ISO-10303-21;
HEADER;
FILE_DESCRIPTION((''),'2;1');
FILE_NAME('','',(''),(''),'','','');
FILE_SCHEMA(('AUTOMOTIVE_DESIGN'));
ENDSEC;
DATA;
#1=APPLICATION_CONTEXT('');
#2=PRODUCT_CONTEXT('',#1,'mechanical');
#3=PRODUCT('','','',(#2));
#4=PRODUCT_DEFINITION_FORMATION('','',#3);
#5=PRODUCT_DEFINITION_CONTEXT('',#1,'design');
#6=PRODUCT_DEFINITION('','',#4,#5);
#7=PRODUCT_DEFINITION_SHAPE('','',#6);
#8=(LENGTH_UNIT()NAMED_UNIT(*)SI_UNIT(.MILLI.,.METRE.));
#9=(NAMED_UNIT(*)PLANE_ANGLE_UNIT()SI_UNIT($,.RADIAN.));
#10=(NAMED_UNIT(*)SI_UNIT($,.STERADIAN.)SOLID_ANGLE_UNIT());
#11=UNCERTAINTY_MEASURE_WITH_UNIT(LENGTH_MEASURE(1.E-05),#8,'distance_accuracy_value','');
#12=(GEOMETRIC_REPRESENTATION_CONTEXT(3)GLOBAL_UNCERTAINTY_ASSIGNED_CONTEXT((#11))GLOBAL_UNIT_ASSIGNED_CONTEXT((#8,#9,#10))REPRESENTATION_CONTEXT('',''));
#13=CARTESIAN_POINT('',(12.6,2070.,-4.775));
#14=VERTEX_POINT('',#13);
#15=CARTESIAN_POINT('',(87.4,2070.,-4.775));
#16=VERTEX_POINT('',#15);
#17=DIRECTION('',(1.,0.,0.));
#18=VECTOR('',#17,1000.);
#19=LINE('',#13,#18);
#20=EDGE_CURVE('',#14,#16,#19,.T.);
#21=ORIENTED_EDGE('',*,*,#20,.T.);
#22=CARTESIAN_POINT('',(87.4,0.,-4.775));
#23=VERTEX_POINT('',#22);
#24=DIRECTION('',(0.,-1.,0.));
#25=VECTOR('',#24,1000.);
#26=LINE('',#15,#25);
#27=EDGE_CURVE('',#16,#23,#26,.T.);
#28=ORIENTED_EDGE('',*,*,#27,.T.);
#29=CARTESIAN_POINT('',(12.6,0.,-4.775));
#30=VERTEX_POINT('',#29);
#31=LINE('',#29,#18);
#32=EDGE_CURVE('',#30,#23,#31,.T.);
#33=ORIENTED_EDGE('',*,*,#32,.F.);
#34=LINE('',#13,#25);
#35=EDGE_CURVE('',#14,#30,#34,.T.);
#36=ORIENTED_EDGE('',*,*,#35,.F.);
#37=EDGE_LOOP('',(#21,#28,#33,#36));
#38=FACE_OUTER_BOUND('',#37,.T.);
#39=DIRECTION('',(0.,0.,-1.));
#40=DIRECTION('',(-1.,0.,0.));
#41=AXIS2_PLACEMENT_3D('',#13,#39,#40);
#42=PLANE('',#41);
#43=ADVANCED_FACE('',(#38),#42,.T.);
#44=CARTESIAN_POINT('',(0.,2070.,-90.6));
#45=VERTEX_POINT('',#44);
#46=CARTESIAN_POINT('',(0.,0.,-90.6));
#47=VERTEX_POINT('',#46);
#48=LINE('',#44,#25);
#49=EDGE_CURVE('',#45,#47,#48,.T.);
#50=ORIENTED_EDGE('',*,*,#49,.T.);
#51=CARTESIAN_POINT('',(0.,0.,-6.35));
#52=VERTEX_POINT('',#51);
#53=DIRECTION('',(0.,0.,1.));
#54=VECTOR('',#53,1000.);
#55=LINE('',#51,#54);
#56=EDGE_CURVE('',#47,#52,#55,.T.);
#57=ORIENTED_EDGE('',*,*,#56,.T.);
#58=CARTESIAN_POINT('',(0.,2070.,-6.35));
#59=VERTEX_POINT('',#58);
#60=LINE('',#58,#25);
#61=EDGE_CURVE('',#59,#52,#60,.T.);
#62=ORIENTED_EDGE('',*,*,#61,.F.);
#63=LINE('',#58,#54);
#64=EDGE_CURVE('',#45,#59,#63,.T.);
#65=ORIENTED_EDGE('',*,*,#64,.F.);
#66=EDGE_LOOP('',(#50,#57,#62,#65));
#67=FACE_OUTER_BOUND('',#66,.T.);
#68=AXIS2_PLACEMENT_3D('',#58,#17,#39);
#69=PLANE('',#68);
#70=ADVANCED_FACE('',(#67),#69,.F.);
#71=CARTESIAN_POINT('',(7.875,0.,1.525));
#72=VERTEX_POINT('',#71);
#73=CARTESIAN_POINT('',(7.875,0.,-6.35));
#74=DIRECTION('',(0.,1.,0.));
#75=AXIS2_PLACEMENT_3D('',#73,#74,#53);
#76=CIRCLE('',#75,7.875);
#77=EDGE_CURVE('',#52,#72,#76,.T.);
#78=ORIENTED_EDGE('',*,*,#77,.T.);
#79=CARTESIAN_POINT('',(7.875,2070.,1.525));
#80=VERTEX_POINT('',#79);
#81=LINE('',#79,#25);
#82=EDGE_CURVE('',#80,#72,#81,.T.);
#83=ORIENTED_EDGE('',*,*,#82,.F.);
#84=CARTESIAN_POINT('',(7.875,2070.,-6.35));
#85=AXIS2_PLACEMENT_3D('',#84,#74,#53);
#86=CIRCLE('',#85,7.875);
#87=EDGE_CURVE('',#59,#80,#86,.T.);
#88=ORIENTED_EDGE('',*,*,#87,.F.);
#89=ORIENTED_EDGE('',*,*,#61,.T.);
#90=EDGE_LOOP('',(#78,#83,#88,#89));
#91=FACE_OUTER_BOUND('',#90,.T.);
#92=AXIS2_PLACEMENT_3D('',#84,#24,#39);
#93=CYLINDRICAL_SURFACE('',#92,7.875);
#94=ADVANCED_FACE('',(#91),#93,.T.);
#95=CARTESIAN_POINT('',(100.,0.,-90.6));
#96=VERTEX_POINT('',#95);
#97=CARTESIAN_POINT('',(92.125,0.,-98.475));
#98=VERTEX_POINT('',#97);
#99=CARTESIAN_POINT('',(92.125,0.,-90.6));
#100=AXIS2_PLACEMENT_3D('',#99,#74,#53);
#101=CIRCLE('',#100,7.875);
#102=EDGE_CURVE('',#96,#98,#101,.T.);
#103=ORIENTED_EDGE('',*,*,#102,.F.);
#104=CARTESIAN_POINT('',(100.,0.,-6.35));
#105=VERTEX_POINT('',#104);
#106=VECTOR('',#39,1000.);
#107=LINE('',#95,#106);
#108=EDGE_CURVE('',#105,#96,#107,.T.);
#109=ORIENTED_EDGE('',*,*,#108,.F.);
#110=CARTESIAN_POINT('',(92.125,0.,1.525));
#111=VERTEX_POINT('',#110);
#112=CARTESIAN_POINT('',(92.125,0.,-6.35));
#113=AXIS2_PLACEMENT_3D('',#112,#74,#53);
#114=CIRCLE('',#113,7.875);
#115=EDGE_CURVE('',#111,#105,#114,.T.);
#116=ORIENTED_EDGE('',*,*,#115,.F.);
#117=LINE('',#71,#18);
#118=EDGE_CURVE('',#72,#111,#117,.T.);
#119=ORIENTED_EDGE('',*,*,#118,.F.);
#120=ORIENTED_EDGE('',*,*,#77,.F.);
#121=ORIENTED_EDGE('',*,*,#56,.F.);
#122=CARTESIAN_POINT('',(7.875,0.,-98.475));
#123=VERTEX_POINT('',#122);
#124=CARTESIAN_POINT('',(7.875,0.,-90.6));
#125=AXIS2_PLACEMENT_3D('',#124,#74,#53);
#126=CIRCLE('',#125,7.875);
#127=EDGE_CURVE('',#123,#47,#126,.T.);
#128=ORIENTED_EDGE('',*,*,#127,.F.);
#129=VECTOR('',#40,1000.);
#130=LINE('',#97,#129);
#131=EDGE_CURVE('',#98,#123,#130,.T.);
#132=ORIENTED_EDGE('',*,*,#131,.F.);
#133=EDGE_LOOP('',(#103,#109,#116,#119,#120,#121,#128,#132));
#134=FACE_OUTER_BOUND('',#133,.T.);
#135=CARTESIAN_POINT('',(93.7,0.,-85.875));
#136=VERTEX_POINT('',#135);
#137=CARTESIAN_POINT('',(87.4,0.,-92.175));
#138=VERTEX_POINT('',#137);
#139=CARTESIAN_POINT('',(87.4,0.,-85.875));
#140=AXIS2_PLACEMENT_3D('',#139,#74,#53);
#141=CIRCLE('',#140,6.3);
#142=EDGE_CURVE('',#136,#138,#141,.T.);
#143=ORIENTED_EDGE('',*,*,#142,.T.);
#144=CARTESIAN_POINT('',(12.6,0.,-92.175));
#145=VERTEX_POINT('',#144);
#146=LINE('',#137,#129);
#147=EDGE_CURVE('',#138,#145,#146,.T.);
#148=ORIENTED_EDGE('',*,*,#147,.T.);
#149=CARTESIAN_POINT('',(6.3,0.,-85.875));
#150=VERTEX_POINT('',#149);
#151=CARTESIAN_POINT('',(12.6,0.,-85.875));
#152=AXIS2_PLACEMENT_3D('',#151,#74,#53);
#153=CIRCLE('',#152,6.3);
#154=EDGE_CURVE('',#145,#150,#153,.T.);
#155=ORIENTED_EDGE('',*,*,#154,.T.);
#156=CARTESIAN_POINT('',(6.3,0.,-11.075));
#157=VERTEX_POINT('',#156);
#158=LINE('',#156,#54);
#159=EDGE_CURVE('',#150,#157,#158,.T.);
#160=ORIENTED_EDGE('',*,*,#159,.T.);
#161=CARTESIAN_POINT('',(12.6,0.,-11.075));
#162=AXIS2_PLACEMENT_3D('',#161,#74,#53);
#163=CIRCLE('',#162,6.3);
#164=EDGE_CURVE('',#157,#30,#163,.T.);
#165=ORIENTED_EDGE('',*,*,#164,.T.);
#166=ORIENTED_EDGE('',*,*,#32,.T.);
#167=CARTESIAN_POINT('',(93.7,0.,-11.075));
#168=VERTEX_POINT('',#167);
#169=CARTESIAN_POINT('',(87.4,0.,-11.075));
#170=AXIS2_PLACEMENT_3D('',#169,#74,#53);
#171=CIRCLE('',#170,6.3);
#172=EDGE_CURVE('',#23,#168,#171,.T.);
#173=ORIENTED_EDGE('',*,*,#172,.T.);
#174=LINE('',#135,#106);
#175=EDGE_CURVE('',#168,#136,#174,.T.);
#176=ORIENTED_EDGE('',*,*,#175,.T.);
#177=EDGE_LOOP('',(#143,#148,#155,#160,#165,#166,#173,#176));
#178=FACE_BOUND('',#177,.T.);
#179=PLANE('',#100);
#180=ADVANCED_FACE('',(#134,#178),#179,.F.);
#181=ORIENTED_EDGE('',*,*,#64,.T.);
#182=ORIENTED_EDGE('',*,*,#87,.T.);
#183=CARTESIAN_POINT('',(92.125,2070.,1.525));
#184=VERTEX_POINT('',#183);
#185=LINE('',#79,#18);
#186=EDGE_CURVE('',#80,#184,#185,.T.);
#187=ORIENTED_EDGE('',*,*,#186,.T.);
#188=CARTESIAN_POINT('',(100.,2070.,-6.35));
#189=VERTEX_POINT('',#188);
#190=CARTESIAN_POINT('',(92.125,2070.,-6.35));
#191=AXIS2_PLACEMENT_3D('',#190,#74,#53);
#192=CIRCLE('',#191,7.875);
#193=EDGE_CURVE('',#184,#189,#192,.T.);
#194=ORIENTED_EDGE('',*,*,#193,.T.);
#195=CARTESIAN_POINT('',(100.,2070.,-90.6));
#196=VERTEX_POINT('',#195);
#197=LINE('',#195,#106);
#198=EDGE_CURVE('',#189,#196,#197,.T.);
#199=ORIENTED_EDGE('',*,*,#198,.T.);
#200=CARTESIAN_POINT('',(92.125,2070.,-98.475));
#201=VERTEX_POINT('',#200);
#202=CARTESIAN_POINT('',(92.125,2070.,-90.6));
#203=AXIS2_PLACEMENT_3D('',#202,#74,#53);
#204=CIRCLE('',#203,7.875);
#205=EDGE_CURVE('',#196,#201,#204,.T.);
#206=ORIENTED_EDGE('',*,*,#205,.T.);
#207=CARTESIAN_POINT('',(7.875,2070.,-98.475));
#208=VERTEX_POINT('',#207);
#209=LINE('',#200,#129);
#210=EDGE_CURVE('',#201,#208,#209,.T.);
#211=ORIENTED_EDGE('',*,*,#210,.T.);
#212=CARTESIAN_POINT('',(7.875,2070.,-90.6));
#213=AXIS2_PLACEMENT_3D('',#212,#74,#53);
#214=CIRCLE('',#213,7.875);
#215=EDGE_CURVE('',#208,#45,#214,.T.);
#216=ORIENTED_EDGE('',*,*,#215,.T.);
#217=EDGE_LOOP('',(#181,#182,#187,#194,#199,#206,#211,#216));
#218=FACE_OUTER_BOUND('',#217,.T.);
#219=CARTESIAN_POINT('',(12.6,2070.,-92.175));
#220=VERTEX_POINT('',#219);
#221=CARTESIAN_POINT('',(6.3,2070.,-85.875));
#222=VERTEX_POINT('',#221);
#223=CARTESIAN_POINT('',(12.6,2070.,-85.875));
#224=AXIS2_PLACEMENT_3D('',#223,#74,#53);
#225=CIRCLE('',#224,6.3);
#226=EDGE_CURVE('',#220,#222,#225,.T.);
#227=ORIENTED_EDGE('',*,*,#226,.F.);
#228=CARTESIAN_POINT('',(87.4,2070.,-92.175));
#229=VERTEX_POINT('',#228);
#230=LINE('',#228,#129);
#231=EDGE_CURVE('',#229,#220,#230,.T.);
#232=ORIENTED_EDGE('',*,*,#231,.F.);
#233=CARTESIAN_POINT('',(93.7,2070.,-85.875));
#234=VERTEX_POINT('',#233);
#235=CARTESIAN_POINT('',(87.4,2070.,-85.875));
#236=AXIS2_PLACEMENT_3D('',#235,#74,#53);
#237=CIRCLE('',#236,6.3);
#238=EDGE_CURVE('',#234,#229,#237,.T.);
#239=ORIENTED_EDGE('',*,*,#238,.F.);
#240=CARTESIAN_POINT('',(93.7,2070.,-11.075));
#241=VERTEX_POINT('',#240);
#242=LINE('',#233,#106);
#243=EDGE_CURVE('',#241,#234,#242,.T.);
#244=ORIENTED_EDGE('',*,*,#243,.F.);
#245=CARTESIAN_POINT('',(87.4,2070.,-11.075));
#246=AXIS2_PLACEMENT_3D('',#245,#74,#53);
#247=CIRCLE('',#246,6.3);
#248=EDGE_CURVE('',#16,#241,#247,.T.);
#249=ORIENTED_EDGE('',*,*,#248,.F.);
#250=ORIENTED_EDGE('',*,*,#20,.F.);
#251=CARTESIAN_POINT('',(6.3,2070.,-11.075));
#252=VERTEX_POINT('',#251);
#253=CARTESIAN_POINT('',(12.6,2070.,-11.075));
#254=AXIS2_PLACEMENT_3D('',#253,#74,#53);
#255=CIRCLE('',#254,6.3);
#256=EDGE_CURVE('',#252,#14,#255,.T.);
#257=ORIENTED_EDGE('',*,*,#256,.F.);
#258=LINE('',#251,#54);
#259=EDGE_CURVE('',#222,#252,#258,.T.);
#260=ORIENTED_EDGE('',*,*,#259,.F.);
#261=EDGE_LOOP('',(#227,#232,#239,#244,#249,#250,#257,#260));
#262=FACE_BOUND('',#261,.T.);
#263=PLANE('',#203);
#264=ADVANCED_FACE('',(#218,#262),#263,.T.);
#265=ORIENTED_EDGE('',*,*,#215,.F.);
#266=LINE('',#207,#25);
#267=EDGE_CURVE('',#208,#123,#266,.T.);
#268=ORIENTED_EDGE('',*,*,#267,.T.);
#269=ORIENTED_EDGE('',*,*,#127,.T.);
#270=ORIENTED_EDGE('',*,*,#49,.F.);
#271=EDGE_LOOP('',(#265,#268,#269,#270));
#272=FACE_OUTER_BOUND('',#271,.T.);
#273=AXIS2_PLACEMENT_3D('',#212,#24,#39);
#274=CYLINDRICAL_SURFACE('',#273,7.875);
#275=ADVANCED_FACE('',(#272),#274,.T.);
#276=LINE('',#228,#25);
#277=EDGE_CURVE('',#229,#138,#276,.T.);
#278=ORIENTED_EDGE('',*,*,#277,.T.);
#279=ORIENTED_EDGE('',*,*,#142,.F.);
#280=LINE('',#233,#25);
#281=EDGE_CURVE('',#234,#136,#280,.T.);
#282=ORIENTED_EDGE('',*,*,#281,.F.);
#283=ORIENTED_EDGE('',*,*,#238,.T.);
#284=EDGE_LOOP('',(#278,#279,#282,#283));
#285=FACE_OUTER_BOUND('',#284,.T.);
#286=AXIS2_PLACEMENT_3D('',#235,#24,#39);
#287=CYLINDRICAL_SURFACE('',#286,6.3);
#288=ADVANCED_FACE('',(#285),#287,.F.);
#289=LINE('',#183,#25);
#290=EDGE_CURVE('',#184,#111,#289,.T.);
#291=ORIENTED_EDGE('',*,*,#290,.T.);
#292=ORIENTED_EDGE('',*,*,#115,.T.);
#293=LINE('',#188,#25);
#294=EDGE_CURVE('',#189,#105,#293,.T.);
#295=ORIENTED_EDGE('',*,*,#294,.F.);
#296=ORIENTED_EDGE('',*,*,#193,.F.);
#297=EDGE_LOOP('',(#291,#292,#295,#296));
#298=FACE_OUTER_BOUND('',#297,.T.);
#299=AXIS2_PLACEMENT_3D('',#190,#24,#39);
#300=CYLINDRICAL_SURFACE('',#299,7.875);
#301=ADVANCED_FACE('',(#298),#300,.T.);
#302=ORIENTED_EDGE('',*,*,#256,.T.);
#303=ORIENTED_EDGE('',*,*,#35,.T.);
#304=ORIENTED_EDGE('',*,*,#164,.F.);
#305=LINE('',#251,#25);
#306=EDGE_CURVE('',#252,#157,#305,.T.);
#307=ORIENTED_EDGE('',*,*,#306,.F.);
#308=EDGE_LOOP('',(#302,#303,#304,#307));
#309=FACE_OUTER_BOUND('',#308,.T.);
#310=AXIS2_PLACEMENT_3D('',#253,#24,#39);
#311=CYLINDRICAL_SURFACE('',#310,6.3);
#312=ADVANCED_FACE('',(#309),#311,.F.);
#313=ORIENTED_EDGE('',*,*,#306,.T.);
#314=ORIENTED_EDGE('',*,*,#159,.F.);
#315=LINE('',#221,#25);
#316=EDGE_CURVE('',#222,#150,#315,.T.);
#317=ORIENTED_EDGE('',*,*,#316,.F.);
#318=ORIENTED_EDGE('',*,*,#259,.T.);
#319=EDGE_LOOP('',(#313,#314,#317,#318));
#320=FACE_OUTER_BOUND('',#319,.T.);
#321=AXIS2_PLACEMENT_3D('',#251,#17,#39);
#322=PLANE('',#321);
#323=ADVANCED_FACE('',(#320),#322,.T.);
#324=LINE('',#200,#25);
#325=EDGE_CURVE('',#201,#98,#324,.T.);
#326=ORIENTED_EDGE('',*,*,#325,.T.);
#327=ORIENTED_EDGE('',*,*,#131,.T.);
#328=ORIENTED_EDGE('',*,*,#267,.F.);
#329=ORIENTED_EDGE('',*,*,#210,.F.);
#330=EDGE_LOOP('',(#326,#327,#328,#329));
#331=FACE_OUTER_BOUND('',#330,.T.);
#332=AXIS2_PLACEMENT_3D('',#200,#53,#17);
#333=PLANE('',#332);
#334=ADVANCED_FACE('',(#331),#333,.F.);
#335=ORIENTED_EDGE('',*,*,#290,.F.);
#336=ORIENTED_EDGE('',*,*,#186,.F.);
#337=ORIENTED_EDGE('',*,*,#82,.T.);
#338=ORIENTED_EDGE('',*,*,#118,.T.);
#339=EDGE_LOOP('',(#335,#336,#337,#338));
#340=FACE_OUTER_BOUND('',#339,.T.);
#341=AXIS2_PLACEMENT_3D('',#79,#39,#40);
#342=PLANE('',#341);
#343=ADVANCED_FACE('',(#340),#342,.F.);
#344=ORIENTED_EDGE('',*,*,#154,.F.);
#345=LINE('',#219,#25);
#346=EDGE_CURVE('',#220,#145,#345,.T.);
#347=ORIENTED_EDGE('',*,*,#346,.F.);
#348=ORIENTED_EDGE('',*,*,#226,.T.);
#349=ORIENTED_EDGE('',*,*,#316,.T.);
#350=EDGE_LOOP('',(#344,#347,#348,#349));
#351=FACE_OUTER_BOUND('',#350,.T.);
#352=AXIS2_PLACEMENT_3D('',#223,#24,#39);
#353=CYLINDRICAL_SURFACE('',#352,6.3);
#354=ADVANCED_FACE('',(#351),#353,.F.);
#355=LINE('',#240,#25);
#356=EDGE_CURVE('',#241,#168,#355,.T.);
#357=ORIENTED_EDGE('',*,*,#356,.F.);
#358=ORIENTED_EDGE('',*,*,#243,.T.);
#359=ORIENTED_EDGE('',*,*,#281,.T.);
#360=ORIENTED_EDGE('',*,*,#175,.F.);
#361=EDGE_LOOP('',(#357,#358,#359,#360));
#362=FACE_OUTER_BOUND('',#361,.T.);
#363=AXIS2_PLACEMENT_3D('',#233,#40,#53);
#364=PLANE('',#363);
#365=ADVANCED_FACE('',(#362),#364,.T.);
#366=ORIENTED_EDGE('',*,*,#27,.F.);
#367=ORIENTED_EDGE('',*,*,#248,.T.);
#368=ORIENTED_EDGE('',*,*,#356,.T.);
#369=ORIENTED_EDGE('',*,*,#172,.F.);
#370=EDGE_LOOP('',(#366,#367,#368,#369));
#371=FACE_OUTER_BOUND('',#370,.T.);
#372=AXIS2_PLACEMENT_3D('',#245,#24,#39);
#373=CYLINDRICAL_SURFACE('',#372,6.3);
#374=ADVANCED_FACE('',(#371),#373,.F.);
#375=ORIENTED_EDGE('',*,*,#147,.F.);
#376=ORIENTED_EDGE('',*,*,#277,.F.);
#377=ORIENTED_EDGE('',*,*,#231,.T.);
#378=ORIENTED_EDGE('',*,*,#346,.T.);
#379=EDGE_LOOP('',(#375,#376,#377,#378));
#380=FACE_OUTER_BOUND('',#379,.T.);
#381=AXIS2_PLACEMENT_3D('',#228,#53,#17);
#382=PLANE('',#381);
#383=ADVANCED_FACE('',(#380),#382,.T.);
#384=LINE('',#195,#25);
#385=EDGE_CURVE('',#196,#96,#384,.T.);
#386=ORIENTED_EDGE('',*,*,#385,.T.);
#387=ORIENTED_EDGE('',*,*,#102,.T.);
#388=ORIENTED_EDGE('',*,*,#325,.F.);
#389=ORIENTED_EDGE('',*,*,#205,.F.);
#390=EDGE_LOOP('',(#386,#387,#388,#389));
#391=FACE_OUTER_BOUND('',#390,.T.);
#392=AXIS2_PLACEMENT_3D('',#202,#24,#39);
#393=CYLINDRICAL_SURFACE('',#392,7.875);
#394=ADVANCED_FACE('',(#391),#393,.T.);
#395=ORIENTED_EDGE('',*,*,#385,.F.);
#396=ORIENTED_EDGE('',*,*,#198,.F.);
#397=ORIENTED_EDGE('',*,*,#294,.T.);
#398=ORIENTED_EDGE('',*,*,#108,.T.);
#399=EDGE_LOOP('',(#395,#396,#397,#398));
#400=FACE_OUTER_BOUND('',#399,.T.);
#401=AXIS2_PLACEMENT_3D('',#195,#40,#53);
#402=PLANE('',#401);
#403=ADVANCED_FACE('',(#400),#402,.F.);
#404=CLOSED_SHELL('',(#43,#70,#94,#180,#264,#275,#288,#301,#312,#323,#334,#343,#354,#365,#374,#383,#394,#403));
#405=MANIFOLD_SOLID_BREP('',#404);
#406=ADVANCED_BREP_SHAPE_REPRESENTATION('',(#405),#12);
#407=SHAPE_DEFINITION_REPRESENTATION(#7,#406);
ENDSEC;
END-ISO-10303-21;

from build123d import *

# Parameters (mm, degrees)
BOSS_EXTRUDE1_DEPTH = 2070


with BuildPart() as part:
    # Sketch2 → Boss-Extrude1 (new body)
    with BuildSketch(Plane(origin=(0, 0, 0), x_dir=(1, 0, 0), z_dir=(0, 1, 0))):
        with BuildLine():
            Line((7.875, -1.525), (92.125, -1.525))
            ThreePointArc((92.125, -1.525), (97.693465902, 0.781534098), (100, 6.35))
            Line((100, 6.35), (100, 90.6))
            ThreePointArc((100, 90.6), (97.693465902, 96.168465902), (92.125, 98.475))
            Line((92.125, 98.475), (7.875, 98.475))
            ThreePointArc((7.875, 98.475), (2.306534098, 96.168465902), (0, 90.6))
            Line((0, 90.6), (0, 6.35))
            ThreePointArc((0, 6.35), (2.306534098, 0.781534098), (7.875, -1.525))
        make_face()
        with BuildLine():
            Line((12.6, 4.775), (87.4, 4.775))
            ThreePointArc((87.4, 4.775), (91.854772721, 6.620227279), (93.7, 11.075))
            Line((93.7, 11.075), (93.7, 85.875))
            ThreePointArc((93.7, 85.875), (91.854772721, 90.329772721), (87.4, 92.175))
            Line((87.4, 92.175), (12.6, 92.175))
            ThreePointArc((12.6, 92.175), (8.145227279, 90.329772721), (6.3, 85.875))
            Line((6.3, 85.875), (6.3, 11.075))
            ThreePointArc((6.3, 11.075), (8.145227279, 6.620227279), (12.6, 4.775))
        make_face(mode=Mode.SUBTRACT)
    extrude(amount=BOSS_EXTRUDE1_DEPTH)


solid = part.part
